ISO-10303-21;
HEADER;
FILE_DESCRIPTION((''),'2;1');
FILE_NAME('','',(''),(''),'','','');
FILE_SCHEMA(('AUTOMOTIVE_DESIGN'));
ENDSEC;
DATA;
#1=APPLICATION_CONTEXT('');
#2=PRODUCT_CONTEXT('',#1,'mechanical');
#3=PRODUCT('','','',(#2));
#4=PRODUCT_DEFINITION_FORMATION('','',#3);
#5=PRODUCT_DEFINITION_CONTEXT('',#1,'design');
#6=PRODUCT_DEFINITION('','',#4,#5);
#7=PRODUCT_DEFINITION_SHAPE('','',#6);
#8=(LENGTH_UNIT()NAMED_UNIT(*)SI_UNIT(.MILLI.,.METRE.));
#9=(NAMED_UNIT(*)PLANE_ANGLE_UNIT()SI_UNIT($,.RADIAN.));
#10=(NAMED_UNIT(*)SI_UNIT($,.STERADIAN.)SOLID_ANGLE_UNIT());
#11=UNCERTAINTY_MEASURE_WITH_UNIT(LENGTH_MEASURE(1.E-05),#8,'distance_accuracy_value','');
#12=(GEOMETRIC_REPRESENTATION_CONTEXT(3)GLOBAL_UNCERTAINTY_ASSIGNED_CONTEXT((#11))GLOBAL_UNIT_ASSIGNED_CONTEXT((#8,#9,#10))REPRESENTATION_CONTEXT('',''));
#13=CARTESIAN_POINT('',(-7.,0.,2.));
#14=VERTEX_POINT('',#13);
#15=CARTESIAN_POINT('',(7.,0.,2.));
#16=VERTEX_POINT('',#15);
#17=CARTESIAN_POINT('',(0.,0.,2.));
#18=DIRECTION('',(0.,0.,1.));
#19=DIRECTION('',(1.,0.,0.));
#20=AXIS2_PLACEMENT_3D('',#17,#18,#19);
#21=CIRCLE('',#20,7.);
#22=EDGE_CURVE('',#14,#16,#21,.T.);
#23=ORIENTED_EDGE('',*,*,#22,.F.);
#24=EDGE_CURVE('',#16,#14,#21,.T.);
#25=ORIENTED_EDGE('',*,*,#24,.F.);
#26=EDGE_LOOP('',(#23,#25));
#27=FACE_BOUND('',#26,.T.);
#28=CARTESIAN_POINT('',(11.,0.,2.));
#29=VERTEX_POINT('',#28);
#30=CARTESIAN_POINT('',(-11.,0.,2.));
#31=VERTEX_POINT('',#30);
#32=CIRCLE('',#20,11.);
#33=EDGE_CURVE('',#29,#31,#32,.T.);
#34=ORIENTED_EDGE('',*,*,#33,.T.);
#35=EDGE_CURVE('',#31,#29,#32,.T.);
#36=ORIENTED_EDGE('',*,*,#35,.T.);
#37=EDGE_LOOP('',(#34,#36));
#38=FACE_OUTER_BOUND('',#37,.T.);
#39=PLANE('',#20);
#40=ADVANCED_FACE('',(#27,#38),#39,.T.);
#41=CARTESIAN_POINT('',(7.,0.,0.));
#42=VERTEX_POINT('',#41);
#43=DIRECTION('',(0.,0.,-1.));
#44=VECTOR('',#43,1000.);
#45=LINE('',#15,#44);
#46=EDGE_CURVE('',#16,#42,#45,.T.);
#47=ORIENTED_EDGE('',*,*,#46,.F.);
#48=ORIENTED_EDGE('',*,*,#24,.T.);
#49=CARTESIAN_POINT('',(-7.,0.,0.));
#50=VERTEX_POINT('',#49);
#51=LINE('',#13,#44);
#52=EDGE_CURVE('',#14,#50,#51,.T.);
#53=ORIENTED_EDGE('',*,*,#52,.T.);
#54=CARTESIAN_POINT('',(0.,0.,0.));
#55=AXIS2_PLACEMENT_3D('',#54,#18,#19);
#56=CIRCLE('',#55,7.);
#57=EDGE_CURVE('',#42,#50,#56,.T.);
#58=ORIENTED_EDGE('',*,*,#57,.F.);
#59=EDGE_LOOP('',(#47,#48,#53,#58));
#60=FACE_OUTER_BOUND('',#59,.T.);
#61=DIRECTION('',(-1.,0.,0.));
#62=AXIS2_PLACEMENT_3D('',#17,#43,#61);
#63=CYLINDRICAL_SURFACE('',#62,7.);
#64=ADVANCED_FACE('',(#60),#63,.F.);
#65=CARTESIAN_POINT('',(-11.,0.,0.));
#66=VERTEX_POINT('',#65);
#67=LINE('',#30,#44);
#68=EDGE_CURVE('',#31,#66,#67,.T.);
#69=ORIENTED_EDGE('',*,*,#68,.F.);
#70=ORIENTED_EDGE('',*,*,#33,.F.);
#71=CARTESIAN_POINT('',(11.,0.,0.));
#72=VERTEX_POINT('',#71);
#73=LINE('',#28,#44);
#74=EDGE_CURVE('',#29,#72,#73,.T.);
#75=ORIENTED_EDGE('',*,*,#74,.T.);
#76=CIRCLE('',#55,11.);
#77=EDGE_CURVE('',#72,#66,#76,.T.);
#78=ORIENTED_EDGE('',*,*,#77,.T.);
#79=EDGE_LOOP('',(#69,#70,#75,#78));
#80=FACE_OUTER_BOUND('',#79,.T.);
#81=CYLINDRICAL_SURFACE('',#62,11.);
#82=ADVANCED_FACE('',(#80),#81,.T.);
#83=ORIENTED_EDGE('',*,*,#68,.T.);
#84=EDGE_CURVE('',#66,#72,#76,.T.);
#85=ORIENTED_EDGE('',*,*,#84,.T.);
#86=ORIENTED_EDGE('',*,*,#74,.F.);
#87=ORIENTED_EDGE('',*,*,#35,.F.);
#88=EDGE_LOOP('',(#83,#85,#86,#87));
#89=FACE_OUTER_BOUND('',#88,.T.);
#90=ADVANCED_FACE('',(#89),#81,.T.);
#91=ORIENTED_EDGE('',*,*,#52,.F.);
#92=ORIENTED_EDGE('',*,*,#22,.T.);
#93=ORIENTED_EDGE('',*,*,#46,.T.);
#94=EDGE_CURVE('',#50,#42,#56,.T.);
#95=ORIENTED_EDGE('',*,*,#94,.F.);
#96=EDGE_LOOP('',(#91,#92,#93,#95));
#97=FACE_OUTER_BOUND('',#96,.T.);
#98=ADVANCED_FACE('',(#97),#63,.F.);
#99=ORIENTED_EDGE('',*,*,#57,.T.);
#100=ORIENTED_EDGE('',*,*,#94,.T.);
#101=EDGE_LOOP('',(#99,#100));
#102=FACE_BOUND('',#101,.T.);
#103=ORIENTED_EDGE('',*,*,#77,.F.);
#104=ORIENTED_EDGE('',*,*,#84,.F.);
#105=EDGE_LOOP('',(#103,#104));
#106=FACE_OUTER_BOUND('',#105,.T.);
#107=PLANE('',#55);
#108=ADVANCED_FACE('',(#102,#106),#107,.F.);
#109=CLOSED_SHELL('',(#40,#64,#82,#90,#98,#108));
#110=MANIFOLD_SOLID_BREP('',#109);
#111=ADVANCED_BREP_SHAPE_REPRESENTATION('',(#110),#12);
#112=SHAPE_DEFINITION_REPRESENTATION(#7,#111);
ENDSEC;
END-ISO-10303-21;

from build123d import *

# Parameters (mm, degrees)
SKETCH1_R           = 11
SKETCH1_R_2         = 7
BOSS_EXTRUDE1_DEPTH = 2


with BuildPart() as part:
    # Sketch1 → Boss-Extrude1 (new body)
    with BuildSketch(Plane.XY):
        Circle(SKETCH1_R)
        Circle(SKETCH1_R_2, mode=Mode.SUBTRACT)
    extrude(amount=BOSS_EXTRUDE1_DEPTH)


solid = part.part
